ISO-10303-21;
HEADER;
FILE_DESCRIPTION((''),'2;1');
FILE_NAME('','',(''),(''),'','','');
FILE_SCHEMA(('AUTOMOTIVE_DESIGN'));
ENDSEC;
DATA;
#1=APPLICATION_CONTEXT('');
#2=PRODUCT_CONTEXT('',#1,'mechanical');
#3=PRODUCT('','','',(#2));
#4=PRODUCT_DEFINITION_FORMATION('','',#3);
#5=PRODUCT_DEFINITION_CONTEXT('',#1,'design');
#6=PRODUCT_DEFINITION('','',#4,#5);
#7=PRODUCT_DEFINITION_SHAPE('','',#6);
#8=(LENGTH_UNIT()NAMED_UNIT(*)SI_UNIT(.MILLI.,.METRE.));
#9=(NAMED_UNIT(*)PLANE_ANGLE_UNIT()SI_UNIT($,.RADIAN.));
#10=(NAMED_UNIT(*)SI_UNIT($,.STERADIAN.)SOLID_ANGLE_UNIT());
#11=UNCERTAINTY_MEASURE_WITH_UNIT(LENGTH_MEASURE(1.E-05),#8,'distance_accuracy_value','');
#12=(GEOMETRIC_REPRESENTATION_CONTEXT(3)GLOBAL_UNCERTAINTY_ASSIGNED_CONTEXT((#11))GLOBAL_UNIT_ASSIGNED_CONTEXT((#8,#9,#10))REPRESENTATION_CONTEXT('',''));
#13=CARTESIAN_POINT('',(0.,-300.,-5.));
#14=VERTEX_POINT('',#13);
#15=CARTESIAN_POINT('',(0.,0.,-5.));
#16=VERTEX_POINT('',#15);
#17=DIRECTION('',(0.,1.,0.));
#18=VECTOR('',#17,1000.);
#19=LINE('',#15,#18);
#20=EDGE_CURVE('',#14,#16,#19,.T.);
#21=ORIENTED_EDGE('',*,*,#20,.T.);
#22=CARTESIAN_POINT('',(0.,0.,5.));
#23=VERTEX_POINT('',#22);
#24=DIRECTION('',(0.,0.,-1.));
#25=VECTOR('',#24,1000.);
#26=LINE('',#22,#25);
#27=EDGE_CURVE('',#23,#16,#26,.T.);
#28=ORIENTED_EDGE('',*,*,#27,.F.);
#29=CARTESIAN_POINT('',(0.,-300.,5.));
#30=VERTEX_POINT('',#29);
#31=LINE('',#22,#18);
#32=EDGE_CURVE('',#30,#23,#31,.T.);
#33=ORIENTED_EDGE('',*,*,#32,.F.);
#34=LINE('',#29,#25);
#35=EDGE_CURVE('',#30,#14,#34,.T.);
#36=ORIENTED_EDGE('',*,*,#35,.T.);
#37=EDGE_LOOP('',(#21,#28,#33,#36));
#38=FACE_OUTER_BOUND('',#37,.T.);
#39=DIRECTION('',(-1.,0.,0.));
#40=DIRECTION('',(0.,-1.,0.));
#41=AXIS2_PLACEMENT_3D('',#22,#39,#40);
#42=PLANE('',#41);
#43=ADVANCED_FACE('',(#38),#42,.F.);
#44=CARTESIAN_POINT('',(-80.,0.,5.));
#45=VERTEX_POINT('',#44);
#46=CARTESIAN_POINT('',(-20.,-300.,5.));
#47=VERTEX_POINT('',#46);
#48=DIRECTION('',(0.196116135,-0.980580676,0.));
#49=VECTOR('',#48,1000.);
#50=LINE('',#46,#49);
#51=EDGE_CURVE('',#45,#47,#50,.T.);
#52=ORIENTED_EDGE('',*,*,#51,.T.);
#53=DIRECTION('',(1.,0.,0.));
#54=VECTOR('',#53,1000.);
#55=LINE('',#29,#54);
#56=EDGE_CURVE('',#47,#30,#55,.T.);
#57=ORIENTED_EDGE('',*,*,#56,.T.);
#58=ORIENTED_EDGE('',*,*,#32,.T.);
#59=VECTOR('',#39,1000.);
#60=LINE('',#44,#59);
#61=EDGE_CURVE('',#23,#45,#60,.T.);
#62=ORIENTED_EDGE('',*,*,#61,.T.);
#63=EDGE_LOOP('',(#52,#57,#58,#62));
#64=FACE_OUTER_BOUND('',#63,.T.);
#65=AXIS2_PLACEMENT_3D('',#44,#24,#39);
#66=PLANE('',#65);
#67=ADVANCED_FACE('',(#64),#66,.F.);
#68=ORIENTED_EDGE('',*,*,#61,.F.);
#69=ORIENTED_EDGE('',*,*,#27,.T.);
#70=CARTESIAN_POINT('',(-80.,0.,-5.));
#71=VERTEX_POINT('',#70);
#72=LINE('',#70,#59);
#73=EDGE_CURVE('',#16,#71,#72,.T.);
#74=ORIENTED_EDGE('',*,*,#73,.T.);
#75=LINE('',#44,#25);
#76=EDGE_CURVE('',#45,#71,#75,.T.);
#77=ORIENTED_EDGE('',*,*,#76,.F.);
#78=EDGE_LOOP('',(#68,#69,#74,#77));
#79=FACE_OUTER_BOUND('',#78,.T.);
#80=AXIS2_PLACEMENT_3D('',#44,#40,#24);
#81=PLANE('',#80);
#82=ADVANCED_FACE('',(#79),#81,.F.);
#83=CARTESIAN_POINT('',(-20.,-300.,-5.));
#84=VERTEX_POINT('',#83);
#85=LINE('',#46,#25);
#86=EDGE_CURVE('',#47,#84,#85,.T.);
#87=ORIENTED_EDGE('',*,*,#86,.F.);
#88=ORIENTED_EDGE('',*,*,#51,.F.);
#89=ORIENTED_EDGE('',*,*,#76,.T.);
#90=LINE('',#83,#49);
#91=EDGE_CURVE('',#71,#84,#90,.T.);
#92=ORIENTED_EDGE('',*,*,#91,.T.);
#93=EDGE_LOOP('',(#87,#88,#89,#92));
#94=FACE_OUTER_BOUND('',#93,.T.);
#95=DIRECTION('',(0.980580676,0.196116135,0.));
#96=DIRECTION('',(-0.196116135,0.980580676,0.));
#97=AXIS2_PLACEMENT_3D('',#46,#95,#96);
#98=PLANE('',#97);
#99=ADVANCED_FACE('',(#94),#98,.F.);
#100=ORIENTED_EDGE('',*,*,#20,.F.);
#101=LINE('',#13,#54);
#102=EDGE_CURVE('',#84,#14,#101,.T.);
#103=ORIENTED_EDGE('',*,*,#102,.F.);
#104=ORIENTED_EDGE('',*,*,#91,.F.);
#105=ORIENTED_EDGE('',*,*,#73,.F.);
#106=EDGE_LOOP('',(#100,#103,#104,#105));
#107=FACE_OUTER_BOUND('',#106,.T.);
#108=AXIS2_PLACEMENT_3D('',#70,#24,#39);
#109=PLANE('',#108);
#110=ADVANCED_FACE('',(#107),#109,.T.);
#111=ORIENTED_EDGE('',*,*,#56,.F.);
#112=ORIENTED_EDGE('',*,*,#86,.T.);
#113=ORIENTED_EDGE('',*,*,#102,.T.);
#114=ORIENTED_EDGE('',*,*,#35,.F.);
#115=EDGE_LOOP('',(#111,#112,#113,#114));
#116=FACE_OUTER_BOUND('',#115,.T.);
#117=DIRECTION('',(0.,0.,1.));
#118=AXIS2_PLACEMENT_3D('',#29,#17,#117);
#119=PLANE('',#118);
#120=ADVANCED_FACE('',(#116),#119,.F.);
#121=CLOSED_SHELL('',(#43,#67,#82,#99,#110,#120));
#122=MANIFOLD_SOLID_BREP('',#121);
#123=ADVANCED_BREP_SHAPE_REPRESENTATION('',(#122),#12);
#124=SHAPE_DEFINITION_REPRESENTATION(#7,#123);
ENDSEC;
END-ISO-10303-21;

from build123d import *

# Parameters (mm, degrees)
EXTRUDE1_DEPTH = 5


with BuildPart() as part:
    # Sketch1 → Extrude1 (new, symmetric)
    with BuildSketch(Plane.XY):
        Polygon((-80, 0), (0, 0), (0, -300), (-20, -300), align=None)
    extrude(amount=EXTRUDE1_DEPTH, both=True)


solid = part.part
